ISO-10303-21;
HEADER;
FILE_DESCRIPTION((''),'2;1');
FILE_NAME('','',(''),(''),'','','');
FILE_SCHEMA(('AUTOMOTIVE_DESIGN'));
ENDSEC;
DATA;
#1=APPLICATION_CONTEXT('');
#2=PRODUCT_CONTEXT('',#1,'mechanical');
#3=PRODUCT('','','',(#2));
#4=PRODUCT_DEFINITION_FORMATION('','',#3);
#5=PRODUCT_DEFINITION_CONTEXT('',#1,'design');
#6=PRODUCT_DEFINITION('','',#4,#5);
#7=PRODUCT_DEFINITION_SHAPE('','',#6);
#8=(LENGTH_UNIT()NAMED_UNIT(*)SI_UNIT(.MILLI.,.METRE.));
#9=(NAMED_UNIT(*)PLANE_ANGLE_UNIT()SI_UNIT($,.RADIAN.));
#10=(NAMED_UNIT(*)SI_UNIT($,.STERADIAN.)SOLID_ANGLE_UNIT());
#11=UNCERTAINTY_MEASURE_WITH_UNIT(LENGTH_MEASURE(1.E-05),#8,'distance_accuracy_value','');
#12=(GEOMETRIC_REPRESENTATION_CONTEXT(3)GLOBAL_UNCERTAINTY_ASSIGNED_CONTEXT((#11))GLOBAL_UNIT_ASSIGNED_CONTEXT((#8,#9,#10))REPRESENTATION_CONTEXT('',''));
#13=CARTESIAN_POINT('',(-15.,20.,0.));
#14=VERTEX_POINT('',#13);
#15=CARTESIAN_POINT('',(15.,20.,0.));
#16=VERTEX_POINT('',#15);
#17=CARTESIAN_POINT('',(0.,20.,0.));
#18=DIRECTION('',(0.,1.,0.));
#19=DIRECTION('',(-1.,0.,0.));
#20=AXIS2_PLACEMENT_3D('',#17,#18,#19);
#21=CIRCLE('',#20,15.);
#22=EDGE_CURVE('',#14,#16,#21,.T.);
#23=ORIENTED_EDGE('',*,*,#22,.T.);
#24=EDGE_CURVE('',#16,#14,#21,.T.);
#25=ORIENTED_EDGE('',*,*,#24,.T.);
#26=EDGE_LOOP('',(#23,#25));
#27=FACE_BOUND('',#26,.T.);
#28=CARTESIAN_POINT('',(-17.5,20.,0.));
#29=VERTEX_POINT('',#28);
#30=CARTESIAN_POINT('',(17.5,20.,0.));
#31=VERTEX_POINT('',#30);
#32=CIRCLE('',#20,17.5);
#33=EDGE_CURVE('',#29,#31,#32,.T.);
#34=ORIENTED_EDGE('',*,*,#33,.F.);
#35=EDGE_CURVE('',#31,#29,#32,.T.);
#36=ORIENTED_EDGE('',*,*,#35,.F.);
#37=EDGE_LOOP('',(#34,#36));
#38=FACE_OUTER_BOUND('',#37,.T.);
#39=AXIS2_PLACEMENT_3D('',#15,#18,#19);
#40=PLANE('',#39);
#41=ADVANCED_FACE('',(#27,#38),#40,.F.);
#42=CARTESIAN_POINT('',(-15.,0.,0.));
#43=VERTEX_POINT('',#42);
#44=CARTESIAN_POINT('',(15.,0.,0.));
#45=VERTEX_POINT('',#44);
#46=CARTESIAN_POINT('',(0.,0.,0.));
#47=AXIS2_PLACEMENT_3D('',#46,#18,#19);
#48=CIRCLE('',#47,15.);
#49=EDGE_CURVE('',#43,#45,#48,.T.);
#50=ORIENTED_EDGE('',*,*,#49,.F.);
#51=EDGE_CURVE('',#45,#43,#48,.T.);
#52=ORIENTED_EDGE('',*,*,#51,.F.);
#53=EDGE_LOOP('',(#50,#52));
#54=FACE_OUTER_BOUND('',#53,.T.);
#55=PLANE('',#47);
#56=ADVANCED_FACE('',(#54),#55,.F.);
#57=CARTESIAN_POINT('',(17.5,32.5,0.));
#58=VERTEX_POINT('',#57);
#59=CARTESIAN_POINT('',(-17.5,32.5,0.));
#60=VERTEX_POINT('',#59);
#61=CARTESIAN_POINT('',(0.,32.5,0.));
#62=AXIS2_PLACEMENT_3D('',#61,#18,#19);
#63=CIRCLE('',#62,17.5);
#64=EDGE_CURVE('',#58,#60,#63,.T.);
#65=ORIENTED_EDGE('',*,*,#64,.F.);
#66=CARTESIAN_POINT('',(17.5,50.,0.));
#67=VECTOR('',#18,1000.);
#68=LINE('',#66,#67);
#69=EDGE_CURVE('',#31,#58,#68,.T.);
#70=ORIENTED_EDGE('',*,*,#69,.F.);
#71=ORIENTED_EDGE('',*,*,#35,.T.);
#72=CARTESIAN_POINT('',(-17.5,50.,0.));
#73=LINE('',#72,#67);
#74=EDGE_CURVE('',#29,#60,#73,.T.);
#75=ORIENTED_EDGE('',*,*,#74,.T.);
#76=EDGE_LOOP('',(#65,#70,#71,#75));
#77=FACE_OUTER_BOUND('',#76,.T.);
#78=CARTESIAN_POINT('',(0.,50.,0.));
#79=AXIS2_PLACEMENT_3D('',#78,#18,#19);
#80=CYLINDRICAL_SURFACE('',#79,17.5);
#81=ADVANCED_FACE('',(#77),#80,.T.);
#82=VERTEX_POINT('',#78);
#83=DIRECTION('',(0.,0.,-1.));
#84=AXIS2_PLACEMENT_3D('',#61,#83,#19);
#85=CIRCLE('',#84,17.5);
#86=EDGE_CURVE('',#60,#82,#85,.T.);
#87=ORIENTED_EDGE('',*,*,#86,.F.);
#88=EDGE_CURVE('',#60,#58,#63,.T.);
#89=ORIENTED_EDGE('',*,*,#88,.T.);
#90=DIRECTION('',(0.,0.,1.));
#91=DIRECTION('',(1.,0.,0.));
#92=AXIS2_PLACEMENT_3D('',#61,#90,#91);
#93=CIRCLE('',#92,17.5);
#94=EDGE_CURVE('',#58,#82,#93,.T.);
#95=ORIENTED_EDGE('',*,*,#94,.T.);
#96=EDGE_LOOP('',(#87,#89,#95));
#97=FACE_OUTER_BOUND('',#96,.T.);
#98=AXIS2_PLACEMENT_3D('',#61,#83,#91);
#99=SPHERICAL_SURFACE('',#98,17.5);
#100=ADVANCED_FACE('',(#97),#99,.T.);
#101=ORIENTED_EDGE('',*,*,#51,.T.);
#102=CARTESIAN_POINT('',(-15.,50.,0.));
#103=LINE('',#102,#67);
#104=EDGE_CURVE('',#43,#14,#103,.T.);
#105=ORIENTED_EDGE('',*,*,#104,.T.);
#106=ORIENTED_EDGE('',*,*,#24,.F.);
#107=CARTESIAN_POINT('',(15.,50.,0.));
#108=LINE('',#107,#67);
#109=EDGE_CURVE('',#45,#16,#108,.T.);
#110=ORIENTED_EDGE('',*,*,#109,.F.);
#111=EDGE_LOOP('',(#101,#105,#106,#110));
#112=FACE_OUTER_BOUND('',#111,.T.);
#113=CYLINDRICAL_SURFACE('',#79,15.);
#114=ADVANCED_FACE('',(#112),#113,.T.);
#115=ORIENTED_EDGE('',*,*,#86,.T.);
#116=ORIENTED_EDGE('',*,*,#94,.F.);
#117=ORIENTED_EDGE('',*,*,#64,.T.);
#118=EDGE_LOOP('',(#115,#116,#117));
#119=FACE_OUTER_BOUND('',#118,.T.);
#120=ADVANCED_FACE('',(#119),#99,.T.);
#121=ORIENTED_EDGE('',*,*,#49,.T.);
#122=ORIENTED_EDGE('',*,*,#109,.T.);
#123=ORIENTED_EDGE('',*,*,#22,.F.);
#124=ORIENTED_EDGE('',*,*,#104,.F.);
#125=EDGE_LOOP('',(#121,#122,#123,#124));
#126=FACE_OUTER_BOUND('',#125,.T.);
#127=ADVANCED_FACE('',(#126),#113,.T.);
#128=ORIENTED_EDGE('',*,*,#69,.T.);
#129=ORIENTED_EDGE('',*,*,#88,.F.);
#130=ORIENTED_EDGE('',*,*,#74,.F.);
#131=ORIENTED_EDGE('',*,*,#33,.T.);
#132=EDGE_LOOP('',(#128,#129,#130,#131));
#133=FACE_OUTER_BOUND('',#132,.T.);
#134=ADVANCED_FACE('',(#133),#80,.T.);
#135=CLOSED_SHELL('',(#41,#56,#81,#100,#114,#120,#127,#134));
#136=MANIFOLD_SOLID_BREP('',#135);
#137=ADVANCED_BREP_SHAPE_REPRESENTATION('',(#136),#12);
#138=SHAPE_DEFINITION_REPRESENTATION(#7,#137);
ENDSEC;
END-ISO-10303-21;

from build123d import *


with BuildPart() as part:
    # Pin Profile Sketch → Pin Body Revolve (revolve)
    with BuildSketch(Plane.XY, mode=Mode.PRIVATE) as pin_body_revolve_sk:
        with BuildLine():
            Line((0, 0), (15, 0))
            Line((15, 0), (15, 20))
            Line((15, 20), (17.5, 20))
            Line((17.5, 20), (17.5, 32.5))
            ThreePointArc((17.5, 32.5), (12.374368671, 44.874368671), (0, 50))
            Line((0, 50), (0, 0))
        make_face()
    revolve(pin_body_revolve_sk.sketch.rotate(Axis((0, 50, 0), (0, -1, 0)), 180), axis=Axis((0, 50, 0), (0, -1, 0)))


solid = part.part
